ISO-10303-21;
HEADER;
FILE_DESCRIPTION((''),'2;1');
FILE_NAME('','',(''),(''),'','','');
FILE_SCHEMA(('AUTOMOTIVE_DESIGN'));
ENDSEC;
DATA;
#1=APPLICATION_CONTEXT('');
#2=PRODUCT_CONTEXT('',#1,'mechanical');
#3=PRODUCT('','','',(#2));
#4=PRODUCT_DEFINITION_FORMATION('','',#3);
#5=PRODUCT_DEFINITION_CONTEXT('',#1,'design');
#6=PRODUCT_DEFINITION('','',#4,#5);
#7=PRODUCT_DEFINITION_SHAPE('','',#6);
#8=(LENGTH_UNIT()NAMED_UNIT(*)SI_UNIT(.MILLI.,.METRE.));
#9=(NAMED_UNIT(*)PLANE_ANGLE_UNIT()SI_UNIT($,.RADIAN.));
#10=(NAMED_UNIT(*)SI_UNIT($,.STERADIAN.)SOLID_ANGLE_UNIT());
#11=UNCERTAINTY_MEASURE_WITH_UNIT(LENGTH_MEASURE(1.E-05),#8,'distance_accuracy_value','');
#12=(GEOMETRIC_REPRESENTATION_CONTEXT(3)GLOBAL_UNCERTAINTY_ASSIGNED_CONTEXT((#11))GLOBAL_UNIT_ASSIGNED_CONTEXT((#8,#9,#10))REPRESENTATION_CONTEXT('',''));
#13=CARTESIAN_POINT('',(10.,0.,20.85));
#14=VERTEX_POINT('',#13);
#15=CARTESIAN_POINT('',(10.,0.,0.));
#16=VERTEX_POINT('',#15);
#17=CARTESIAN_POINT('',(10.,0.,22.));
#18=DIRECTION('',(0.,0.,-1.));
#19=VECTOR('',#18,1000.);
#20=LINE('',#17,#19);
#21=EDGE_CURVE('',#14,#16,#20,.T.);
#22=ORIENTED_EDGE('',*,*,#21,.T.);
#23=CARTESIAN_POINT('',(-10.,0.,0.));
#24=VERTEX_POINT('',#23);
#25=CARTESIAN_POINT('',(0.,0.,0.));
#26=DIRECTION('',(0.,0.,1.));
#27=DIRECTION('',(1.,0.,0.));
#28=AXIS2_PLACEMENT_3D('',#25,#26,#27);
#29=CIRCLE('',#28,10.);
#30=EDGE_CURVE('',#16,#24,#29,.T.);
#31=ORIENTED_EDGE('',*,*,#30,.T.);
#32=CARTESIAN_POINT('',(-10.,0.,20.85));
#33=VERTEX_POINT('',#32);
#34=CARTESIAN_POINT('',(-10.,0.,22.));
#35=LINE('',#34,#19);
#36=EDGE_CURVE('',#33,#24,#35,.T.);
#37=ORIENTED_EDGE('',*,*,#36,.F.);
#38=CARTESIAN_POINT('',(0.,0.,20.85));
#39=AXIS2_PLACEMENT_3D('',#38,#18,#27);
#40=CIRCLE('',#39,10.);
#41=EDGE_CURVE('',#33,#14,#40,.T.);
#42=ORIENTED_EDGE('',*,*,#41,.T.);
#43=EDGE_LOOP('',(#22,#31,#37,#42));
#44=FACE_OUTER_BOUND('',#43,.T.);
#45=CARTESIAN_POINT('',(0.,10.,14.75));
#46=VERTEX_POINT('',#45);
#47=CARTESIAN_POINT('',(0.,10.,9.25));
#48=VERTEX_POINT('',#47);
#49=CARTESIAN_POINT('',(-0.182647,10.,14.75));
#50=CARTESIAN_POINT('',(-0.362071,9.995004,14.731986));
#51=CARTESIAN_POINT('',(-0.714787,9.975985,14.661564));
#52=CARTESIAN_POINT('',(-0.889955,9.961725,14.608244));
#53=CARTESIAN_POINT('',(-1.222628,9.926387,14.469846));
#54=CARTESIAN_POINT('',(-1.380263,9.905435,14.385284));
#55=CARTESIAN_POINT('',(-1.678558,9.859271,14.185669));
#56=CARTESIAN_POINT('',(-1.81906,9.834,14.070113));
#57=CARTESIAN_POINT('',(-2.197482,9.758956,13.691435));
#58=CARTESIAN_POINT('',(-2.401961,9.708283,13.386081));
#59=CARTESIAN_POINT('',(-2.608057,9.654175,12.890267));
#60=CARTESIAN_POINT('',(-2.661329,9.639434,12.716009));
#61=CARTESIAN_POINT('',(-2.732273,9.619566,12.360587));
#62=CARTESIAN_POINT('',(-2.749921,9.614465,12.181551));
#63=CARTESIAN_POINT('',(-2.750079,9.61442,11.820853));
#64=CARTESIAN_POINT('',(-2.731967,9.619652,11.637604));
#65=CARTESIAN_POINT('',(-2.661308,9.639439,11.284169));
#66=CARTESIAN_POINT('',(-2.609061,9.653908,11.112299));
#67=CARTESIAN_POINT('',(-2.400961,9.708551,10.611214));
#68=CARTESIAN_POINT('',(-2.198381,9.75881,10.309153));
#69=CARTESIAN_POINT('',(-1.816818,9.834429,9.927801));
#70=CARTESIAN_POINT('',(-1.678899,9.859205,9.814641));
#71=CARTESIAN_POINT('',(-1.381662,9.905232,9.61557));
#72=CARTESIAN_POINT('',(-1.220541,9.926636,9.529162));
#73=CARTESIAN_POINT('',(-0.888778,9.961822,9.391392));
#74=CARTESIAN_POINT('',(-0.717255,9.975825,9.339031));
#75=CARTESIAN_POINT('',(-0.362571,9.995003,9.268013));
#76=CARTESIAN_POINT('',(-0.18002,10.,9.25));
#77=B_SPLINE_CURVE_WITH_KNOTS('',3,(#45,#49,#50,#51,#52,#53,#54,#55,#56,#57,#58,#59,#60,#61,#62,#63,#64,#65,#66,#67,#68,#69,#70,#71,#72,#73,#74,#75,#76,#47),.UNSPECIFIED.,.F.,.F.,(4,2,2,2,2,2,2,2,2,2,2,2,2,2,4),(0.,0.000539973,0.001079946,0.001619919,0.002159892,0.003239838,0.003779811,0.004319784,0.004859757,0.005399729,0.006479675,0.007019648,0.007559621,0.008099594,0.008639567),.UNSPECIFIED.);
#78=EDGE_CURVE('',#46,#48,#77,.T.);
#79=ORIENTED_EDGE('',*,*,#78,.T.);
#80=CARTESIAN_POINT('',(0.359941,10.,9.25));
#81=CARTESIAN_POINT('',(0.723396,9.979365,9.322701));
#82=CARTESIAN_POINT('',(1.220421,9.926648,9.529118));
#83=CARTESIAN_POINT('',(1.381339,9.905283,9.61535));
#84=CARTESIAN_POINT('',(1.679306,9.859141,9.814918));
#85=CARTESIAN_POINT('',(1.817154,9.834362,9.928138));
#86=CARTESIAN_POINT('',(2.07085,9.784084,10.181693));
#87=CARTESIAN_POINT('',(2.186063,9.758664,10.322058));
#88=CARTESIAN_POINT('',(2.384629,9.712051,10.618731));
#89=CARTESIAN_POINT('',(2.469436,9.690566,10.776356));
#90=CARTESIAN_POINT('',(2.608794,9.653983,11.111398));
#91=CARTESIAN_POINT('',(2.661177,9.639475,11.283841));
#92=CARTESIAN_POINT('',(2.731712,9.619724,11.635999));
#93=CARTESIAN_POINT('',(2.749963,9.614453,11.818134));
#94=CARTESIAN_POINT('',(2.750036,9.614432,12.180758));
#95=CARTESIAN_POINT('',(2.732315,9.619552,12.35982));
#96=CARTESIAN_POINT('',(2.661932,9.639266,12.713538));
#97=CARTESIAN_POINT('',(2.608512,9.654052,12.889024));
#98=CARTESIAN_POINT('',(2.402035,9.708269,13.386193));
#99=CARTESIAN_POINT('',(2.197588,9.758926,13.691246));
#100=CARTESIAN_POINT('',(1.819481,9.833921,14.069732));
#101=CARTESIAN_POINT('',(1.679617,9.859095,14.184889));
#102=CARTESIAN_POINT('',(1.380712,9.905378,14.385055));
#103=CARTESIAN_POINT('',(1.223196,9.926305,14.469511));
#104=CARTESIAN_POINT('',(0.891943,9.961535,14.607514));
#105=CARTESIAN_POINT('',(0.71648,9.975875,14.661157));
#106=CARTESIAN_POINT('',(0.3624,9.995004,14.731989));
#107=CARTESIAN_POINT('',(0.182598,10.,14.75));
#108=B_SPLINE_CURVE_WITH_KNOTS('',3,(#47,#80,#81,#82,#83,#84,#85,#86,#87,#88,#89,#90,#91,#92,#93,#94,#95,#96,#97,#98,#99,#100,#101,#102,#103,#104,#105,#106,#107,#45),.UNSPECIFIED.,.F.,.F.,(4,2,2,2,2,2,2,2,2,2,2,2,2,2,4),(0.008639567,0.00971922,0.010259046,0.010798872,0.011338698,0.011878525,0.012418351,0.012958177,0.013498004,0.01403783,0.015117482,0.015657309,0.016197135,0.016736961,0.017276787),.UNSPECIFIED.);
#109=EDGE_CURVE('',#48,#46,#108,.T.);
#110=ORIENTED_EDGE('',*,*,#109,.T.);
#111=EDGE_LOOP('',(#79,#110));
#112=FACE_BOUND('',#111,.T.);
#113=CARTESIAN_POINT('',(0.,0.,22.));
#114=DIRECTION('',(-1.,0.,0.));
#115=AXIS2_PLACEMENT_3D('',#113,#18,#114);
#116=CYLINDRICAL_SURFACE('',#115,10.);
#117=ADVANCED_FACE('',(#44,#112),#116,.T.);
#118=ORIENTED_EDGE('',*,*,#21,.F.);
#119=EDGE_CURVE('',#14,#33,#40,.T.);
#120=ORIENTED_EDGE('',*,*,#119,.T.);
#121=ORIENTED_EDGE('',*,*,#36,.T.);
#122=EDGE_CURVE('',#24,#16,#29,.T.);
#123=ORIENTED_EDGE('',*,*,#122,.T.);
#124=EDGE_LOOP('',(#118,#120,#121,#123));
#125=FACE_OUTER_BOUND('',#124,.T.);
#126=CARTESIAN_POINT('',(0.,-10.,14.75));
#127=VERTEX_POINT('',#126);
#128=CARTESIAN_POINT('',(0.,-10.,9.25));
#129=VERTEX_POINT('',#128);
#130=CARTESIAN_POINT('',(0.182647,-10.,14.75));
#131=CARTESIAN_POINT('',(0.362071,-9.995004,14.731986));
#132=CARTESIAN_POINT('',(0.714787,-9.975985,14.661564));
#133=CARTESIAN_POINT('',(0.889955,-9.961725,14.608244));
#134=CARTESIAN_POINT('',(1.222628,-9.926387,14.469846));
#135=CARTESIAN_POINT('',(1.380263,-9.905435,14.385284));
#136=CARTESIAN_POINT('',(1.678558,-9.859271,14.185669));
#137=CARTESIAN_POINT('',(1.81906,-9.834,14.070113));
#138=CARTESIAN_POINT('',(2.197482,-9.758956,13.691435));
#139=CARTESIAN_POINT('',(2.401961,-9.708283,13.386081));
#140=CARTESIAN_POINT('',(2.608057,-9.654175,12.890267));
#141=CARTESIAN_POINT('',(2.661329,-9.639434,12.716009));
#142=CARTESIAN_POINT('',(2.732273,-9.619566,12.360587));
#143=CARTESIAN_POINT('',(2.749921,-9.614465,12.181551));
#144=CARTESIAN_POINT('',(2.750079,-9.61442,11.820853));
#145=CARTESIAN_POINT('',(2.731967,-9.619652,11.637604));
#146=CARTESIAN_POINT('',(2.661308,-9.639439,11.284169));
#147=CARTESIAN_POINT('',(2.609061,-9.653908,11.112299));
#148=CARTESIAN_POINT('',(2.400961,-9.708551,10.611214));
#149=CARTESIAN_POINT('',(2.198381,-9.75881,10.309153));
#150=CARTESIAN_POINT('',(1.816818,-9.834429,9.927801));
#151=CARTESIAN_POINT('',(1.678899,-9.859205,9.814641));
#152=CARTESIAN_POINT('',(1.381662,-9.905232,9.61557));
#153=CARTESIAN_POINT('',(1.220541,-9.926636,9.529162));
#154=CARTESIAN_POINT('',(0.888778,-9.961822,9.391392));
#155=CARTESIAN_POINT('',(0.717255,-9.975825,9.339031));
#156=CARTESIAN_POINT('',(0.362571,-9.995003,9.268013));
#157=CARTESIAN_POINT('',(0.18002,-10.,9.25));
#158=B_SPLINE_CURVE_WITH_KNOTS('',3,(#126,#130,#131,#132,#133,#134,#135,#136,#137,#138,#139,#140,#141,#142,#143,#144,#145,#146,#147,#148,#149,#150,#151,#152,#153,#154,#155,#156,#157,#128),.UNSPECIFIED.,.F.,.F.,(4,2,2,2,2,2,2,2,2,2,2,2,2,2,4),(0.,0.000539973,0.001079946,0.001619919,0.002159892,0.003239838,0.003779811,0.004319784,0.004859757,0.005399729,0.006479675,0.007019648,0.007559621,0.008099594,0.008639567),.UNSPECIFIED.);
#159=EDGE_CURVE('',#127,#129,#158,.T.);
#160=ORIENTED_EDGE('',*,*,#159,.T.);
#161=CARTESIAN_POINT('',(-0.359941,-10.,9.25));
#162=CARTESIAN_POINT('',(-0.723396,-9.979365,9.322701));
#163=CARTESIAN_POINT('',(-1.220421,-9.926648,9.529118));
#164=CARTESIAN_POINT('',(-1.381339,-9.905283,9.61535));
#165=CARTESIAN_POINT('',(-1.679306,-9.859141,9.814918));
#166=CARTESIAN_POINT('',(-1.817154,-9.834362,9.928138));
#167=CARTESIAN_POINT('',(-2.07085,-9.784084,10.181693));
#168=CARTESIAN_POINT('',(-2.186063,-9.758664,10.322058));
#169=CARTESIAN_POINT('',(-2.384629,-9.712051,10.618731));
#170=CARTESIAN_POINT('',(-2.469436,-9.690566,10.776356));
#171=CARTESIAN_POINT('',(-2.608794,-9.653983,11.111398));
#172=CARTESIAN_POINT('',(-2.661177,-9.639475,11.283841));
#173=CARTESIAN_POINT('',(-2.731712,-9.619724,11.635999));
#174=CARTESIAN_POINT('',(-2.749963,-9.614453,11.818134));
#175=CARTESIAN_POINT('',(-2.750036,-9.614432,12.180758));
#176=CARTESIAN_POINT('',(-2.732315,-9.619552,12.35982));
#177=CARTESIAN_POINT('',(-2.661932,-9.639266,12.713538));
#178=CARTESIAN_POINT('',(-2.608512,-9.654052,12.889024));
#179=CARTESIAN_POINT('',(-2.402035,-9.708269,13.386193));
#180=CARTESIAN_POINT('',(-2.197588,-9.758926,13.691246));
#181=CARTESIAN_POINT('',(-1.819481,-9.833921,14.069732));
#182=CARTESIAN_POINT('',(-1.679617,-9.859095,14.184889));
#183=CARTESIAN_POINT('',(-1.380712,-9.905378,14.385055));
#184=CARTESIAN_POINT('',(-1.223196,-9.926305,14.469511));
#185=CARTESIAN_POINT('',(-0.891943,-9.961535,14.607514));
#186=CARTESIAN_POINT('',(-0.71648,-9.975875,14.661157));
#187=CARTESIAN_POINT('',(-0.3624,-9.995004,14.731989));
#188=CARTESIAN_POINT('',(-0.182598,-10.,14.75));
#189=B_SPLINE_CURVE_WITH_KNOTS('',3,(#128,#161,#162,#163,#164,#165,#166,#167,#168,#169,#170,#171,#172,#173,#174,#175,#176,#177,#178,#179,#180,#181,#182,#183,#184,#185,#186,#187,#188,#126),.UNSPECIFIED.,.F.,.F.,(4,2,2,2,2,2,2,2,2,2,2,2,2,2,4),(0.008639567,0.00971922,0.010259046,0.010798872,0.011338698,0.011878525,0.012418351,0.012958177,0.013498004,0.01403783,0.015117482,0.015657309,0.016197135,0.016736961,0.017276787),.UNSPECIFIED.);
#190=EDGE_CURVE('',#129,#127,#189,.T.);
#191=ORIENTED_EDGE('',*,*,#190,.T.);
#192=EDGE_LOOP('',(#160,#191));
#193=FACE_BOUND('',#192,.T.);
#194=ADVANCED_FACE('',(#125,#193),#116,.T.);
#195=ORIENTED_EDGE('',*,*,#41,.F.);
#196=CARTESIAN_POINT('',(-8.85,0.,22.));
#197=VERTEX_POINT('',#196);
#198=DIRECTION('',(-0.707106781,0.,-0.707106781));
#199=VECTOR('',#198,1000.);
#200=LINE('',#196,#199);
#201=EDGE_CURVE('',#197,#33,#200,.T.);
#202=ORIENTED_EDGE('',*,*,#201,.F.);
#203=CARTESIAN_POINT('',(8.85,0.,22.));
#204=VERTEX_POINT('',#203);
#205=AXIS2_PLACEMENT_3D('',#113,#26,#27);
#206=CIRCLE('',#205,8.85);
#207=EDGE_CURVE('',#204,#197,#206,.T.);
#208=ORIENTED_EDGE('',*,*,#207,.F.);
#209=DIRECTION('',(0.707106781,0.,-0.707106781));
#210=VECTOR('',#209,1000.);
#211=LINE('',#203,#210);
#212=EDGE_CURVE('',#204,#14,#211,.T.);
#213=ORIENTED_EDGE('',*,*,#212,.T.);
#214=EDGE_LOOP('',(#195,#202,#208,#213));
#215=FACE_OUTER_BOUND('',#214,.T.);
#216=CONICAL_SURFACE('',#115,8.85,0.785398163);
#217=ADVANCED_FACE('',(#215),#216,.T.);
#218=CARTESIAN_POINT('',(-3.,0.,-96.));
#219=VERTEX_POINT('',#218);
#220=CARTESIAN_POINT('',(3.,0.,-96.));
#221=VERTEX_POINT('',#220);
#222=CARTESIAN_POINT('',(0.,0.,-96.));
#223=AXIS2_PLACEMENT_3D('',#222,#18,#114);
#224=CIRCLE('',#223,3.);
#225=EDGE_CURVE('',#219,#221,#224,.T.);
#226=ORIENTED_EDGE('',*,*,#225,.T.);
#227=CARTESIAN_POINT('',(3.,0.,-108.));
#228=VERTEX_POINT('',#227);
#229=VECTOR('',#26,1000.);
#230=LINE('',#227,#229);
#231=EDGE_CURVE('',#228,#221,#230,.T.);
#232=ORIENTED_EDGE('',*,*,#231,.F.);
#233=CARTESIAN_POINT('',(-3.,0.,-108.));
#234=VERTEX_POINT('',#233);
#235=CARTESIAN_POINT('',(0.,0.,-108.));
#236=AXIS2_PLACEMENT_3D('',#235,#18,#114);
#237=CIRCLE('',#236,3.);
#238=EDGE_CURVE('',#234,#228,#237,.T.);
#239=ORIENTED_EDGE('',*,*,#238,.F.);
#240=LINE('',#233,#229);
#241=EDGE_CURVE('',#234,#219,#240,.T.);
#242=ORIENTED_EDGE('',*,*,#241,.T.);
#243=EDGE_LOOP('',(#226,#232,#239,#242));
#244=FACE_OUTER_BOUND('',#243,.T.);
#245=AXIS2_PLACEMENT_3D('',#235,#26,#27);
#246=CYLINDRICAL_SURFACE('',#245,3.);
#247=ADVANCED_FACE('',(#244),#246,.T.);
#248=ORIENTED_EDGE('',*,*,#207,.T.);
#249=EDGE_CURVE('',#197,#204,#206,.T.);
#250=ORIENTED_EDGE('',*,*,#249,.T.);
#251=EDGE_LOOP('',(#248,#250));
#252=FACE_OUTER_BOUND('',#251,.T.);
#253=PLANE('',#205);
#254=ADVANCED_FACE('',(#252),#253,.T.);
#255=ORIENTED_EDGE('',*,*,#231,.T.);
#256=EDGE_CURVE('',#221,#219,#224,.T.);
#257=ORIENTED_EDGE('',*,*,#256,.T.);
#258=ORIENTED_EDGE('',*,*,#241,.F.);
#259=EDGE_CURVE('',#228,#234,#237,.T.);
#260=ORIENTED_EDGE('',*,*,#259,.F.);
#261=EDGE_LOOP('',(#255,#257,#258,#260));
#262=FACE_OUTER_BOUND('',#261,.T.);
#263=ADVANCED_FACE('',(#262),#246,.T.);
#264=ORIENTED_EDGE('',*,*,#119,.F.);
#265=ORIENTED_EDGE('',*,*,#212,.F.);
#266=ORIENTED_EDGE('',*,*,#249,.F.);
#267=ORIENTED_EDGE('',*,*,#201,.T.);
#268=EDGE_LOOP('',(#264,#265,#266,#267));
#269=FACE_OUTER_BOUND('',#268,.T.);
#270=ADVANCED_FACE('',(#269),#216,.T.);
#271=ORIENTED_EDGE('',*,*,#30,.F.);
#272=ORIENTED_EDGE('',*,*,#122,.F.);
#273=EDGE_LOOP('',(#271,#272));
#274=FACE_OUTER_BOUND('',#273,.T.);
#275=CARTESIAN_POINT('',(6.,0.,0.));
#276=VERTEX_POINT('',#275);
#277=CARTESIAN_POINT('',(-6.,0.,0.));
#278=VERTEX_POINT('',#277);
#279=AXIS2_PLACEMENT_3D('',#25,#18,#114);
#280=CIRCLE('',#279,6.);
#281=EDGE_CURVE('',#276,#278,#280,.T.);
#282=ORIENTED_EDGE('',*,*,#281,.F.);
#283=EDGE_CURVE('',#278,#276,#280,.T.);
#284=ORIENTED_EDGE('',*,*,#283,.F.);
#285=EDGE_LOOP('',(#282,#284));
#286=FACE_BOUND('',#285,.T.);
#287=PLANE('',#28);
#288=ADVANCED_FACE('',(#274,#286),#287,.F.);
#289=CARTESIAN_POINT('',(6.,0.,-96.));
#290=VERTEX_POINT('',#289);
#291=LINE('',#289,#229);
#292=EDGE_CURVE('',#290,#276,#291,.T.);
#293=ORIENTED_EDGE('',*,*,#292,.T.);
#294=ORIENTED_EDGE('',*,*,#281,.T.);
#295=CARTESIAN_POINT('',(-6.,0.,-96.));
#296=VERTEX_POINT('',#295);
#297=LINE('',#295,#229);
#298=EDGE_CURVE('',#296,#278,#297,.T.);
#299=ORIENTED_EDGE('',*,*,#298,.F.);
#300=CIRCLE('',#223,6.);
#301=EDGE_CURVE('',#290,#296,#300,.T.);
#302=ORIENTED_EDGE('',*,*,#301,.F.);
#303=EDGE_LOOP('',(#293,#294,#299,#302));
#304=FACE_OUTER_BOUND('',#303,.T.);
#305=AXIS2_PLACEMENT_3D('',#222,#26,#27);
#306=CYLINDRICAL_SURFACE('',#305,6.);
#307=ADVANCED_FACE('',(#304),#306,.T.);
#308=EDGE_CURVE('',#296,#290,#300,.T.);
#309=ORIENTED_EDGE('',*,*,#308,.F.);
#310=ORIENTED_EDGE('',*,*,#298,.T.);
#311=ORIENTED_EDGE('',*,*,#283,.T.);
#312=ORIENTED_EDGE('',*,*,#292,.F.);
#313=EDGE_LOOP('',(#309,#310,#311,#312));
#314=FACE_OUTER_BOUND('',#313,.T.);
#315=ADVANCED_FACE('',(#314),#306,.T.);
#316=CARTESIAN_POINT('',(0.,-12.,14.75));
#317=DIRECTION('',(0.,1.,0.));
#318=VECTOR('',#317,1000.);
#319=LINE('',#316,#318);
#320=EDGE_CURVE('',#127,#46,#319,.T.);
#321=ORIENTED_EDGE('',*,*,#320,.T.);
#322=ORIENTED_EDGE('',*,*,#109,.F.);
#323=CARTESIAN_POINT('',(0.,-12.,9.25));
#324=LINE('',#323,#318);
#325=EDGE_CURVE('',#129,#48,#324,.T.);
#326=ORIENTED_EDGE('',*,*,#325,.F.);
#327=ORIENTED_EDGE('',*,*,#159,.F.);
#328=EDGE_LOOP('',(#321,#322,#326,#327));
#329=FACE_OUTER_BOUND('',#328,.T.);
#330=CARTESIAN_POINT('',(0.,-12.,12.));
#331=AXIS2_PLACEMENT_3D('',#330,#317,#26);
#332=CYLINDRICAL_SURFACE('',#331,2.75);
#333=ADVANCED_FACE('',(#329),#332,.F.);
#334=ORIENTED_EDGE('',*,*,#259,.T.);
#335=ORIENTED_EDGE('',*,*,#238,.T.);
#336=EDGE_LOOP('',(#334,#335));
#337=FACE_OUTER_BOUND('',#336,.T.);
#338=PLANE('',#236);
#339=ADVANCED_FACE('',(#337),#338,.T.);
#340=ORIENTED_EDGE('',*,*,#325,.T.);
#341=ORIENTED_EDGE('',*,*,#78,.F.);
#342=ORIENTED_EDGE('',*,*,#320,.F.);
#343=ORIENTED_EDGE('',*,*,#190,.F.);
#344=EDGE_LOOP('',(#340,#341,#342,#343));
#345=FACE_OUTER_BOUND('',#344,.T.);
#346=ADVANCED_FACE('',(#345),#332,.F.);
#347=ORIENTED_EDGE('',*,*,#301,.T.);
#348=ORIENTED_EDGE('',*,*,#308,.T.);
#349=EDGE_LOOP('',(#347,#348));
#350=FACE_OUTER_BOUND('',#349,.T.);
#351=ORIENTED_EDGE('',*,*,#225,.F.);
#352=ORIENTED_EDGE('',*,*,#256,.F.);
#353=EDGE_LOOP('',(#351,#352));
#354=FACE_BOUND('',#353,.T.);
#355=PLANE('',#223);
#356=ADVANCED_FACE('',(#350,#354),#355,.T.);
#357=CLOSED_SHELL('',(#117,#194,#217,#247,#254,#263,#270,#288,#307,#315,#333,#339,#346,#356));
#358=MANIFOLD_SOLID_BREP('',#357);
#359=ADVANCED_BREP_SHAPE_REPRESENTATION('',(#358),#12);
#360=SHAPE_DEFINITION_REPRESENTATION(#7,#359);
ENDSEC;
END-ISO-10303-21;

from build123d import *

# Parameters (mm, degrees)
HEAD_PROFILE_20_R          = 10
HEAD_20X22_DEPTH           = 22
SHANK_PROFILE_12_R         = 6
THREADED_SHANK_12X96_DEPTH = 96
PILOT_PROFILE_6_R          = 3
PILOT_TIP_6X12_DEPTH       = 12
CROSS_HOLE_PROFILE_5_5_R   = 2.75
CROSS_HOLE_5_5_DEPTH       = 12
HEAD_CHAMFER_1_15X45_SIZE  = 1.15


with BuildPart() as part:
    # Head Profile Ø20 → Head Ø20x22 (new body)
    with BuildSketch(Plane.XY):
        Circle(HEAD_PROFILE_20_R)
    extrude(amount=HEAD_20X22_DEPTH)

    # Shank Profile Ø12 → Threaded Shank Ø12x96 (add)
    with BuildSketch(Plane(origin=(0, 0, 0), x_dir=(-1, 0, 0), z_dir=(0, 0, -1))):
        Circle(SHANK_PROFILE_12_R)
    extrude(amount=THREADED_SHANK_12X96_DEPTH)

    # Pilot Profile Ø6 → Pilot Tip Ø6x12 (add)
    with BuildSketch(Plane(origin=(0, 0, -96), x_dir=(-1, 0, 0), z_dir=(0, 0, -1))):
        Circle(PILOT_PROFILE_6_R)
    extrude(amount=PILOT_TIP_6X12_DEPTH)

    # Cross Hole Profile Ø5.5 → Cross Hole Ø5.5 (cut, symmetric)
    with BuildSketch(Plane(origin=(0, 0, 0), x_dir=(1, 0, 0), z_dir=(0, 1, 0))):
        with Locations(Location((0, -12, 0), (0, 0, 270))):
            Circle(CROSS_HOLE_PROFILE_5_5_R)
    extrude(amount=CROSS_HOLE_5_5_DEPTH, both=True, mode=Mode.SUBTRACT)

    # Head Chamfer 1.15x45
    head_chamfer_1_15x45_edges = [part.edges().sort_by_distance(p)[0] for p in [
        (-10, 0, 22),
    ]]
    chamfer(head_chamfer_1_15x45_edges, length=HEAD_CHAMFER_1_15X45_SIZE)


solid = part.part
